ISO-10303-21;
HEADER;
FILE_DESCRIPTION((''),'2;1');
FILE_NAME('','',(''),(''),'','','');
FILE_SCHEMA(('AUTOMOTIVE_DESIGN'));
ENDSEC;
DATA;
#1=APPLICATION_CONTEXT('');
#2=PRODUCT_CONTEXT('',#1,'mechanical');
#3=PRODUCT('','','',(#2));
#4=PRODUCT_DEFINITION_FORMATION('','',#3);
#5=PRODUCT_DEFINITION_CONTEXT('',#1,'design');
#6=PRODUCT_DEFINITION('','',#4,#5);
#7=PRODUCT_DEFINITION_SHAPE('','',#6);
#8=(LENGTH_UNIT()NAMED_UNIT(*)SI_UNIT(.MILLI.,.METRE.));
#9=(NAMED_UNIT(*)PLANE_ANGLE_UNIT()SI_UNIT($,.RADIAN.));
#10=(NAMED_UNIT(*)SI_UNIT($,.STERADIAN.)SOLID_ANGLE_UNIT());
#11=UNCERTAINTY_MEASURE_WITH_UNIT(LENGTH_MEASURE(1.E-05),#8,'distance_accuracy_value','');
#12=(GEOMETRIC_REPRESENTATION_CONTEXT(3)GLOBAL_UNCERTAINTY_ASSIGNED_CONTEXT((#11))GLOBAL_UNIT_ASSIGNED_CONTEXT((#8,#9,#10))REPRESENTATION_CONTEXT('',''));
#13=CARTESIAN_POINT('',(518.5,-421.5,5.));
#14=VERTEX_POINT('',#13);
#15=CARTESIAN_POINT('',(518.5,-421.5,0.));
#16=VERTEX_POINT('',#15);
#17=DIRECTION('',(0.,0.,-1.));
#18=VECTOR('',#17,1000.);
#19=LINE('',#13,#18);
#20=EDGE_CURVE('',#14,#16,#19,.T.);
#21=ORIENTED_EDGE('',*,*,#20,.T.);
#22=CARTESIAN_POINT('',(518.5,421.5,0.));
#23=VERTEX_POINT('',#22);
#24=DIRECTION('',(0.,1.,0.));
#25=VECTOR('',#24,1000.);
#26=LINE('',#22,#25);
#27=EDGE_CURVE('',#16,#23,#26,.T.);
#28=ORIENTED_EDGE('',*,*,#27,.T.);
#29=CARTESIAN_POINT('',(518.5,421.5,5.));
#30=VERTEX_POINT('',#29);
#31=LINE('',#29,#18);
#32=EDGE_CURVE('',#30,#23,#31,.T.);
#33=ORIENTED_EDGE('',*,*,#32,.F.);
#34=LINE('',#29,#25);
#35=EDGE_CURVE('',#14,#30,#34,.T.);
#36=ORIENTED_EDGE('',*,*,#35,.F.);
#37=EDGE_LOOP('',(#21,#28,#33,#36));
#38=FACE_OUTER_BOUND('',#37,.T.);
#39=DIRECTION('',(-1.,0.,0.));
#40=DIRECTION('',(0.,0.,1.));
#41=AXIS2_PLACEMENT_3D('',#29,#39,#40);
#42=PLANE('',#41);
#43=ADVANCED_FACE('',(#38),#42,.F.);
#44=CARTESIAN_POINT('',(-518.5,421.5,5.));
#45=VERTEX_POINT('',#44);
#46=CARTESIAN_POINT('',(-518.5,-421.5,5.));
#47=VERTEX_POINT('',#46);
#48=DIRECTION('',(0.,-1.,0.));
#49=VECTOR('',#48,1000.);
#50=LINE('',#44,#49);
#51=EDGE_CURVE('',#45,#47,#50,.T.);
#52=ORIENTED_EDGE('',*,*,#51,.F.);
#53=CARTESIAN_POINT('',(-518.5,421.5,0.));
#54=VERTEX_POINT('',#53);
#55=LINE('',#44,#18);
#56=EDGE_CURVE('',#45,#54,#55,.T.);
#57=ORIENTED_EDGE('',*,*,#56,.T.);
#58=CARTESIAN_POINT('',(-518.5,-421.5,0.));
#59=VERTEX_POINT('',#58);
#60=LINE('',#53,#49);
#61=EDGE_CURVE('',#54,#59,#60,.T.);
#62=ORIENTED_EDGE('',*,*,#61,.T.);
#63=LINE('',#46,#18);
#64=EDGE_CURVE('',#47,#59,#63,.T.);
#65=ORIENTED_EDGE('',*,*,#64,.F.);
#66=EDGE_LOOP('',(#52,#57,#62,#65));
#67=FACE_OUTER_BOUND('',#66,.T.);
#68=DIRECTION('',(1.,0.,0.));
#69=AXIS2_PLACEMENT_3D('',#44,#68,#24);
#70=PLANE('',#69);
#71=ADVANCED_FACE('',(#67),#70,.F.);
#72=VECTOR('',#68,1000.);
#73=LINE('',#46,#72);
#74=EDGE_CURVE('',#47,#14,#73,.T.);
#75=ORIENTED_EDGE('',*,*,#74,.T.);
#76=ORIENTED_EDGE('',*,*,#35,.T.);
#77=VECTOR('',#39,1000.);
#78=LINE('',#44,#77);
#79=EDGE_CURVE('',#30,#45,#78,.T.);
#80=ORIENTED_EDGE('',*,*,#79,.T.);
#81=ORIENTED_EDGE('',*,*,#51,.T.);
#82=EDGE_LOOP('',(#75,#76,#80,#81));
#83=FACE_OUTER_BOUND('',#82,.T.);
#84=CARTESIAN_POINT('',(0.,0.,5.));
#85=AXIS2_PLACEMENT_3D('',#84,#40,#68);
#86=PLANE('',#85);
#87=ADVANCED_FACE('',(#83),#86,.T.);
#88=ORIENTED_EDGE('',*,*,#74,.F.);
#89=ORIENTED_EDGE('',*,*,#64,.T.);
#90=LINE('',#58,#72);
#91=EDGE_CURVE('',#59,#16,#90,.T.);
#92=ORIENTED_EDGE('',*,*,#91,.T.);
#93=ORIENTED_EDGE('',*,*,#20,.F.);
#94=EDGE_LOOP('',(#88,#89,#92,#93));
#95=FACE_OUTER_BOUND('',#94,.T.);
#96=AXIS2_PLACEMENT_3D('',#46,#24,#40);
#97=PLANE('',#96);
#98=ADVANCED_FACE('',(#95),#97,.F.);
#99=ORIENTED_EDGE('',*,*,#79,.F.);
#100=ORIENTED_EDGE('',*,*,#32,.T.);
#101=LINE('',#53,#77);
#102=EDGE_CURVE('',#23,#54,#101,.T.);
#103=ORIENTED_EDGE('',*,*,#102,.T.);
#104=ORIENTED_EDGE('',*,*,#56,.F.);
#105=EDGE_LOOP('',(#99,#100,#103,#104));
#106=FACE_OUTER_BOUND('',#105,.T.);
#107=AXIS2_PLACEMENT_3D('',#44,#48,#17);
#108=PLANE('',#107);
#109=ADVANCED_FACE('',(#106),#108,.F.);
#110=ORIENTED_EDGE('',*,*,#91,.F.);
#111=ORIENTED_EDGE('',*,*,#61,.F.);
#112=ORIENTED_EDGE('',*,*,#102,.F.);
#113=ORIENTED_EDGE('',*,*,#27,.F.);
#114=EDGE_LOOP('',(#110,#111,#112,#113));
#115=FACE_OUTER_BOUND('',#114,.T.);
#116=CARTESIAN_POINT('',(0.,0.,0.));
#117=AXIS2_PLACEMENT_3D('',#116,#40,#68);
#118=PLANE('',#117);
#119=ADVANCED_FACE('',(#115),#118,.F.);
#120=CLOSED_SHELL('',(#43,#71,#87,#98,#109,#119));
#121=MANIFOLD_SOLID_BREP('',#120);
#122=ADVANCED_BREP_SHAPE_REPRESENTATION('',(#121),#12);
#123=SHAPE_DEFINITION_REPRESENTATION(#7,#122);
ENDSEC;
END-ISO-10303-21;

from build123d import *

# Parameters (mm, degrees)
SKETCH_1_W      = 1037
SKETCH_1_H      = 843
EXTRUDE_1_DEPTH = 5


with BuildPart() as part:
    # 草图1 → 凸台-拉伸1 (new body)
    with BuildSketch(Plane.XY):
        Rectangle(SKETCH_1_W, SKETCH_1_H)
    extrude(amount=EXTRUDE_1_DEPTH)


solid = part.part
